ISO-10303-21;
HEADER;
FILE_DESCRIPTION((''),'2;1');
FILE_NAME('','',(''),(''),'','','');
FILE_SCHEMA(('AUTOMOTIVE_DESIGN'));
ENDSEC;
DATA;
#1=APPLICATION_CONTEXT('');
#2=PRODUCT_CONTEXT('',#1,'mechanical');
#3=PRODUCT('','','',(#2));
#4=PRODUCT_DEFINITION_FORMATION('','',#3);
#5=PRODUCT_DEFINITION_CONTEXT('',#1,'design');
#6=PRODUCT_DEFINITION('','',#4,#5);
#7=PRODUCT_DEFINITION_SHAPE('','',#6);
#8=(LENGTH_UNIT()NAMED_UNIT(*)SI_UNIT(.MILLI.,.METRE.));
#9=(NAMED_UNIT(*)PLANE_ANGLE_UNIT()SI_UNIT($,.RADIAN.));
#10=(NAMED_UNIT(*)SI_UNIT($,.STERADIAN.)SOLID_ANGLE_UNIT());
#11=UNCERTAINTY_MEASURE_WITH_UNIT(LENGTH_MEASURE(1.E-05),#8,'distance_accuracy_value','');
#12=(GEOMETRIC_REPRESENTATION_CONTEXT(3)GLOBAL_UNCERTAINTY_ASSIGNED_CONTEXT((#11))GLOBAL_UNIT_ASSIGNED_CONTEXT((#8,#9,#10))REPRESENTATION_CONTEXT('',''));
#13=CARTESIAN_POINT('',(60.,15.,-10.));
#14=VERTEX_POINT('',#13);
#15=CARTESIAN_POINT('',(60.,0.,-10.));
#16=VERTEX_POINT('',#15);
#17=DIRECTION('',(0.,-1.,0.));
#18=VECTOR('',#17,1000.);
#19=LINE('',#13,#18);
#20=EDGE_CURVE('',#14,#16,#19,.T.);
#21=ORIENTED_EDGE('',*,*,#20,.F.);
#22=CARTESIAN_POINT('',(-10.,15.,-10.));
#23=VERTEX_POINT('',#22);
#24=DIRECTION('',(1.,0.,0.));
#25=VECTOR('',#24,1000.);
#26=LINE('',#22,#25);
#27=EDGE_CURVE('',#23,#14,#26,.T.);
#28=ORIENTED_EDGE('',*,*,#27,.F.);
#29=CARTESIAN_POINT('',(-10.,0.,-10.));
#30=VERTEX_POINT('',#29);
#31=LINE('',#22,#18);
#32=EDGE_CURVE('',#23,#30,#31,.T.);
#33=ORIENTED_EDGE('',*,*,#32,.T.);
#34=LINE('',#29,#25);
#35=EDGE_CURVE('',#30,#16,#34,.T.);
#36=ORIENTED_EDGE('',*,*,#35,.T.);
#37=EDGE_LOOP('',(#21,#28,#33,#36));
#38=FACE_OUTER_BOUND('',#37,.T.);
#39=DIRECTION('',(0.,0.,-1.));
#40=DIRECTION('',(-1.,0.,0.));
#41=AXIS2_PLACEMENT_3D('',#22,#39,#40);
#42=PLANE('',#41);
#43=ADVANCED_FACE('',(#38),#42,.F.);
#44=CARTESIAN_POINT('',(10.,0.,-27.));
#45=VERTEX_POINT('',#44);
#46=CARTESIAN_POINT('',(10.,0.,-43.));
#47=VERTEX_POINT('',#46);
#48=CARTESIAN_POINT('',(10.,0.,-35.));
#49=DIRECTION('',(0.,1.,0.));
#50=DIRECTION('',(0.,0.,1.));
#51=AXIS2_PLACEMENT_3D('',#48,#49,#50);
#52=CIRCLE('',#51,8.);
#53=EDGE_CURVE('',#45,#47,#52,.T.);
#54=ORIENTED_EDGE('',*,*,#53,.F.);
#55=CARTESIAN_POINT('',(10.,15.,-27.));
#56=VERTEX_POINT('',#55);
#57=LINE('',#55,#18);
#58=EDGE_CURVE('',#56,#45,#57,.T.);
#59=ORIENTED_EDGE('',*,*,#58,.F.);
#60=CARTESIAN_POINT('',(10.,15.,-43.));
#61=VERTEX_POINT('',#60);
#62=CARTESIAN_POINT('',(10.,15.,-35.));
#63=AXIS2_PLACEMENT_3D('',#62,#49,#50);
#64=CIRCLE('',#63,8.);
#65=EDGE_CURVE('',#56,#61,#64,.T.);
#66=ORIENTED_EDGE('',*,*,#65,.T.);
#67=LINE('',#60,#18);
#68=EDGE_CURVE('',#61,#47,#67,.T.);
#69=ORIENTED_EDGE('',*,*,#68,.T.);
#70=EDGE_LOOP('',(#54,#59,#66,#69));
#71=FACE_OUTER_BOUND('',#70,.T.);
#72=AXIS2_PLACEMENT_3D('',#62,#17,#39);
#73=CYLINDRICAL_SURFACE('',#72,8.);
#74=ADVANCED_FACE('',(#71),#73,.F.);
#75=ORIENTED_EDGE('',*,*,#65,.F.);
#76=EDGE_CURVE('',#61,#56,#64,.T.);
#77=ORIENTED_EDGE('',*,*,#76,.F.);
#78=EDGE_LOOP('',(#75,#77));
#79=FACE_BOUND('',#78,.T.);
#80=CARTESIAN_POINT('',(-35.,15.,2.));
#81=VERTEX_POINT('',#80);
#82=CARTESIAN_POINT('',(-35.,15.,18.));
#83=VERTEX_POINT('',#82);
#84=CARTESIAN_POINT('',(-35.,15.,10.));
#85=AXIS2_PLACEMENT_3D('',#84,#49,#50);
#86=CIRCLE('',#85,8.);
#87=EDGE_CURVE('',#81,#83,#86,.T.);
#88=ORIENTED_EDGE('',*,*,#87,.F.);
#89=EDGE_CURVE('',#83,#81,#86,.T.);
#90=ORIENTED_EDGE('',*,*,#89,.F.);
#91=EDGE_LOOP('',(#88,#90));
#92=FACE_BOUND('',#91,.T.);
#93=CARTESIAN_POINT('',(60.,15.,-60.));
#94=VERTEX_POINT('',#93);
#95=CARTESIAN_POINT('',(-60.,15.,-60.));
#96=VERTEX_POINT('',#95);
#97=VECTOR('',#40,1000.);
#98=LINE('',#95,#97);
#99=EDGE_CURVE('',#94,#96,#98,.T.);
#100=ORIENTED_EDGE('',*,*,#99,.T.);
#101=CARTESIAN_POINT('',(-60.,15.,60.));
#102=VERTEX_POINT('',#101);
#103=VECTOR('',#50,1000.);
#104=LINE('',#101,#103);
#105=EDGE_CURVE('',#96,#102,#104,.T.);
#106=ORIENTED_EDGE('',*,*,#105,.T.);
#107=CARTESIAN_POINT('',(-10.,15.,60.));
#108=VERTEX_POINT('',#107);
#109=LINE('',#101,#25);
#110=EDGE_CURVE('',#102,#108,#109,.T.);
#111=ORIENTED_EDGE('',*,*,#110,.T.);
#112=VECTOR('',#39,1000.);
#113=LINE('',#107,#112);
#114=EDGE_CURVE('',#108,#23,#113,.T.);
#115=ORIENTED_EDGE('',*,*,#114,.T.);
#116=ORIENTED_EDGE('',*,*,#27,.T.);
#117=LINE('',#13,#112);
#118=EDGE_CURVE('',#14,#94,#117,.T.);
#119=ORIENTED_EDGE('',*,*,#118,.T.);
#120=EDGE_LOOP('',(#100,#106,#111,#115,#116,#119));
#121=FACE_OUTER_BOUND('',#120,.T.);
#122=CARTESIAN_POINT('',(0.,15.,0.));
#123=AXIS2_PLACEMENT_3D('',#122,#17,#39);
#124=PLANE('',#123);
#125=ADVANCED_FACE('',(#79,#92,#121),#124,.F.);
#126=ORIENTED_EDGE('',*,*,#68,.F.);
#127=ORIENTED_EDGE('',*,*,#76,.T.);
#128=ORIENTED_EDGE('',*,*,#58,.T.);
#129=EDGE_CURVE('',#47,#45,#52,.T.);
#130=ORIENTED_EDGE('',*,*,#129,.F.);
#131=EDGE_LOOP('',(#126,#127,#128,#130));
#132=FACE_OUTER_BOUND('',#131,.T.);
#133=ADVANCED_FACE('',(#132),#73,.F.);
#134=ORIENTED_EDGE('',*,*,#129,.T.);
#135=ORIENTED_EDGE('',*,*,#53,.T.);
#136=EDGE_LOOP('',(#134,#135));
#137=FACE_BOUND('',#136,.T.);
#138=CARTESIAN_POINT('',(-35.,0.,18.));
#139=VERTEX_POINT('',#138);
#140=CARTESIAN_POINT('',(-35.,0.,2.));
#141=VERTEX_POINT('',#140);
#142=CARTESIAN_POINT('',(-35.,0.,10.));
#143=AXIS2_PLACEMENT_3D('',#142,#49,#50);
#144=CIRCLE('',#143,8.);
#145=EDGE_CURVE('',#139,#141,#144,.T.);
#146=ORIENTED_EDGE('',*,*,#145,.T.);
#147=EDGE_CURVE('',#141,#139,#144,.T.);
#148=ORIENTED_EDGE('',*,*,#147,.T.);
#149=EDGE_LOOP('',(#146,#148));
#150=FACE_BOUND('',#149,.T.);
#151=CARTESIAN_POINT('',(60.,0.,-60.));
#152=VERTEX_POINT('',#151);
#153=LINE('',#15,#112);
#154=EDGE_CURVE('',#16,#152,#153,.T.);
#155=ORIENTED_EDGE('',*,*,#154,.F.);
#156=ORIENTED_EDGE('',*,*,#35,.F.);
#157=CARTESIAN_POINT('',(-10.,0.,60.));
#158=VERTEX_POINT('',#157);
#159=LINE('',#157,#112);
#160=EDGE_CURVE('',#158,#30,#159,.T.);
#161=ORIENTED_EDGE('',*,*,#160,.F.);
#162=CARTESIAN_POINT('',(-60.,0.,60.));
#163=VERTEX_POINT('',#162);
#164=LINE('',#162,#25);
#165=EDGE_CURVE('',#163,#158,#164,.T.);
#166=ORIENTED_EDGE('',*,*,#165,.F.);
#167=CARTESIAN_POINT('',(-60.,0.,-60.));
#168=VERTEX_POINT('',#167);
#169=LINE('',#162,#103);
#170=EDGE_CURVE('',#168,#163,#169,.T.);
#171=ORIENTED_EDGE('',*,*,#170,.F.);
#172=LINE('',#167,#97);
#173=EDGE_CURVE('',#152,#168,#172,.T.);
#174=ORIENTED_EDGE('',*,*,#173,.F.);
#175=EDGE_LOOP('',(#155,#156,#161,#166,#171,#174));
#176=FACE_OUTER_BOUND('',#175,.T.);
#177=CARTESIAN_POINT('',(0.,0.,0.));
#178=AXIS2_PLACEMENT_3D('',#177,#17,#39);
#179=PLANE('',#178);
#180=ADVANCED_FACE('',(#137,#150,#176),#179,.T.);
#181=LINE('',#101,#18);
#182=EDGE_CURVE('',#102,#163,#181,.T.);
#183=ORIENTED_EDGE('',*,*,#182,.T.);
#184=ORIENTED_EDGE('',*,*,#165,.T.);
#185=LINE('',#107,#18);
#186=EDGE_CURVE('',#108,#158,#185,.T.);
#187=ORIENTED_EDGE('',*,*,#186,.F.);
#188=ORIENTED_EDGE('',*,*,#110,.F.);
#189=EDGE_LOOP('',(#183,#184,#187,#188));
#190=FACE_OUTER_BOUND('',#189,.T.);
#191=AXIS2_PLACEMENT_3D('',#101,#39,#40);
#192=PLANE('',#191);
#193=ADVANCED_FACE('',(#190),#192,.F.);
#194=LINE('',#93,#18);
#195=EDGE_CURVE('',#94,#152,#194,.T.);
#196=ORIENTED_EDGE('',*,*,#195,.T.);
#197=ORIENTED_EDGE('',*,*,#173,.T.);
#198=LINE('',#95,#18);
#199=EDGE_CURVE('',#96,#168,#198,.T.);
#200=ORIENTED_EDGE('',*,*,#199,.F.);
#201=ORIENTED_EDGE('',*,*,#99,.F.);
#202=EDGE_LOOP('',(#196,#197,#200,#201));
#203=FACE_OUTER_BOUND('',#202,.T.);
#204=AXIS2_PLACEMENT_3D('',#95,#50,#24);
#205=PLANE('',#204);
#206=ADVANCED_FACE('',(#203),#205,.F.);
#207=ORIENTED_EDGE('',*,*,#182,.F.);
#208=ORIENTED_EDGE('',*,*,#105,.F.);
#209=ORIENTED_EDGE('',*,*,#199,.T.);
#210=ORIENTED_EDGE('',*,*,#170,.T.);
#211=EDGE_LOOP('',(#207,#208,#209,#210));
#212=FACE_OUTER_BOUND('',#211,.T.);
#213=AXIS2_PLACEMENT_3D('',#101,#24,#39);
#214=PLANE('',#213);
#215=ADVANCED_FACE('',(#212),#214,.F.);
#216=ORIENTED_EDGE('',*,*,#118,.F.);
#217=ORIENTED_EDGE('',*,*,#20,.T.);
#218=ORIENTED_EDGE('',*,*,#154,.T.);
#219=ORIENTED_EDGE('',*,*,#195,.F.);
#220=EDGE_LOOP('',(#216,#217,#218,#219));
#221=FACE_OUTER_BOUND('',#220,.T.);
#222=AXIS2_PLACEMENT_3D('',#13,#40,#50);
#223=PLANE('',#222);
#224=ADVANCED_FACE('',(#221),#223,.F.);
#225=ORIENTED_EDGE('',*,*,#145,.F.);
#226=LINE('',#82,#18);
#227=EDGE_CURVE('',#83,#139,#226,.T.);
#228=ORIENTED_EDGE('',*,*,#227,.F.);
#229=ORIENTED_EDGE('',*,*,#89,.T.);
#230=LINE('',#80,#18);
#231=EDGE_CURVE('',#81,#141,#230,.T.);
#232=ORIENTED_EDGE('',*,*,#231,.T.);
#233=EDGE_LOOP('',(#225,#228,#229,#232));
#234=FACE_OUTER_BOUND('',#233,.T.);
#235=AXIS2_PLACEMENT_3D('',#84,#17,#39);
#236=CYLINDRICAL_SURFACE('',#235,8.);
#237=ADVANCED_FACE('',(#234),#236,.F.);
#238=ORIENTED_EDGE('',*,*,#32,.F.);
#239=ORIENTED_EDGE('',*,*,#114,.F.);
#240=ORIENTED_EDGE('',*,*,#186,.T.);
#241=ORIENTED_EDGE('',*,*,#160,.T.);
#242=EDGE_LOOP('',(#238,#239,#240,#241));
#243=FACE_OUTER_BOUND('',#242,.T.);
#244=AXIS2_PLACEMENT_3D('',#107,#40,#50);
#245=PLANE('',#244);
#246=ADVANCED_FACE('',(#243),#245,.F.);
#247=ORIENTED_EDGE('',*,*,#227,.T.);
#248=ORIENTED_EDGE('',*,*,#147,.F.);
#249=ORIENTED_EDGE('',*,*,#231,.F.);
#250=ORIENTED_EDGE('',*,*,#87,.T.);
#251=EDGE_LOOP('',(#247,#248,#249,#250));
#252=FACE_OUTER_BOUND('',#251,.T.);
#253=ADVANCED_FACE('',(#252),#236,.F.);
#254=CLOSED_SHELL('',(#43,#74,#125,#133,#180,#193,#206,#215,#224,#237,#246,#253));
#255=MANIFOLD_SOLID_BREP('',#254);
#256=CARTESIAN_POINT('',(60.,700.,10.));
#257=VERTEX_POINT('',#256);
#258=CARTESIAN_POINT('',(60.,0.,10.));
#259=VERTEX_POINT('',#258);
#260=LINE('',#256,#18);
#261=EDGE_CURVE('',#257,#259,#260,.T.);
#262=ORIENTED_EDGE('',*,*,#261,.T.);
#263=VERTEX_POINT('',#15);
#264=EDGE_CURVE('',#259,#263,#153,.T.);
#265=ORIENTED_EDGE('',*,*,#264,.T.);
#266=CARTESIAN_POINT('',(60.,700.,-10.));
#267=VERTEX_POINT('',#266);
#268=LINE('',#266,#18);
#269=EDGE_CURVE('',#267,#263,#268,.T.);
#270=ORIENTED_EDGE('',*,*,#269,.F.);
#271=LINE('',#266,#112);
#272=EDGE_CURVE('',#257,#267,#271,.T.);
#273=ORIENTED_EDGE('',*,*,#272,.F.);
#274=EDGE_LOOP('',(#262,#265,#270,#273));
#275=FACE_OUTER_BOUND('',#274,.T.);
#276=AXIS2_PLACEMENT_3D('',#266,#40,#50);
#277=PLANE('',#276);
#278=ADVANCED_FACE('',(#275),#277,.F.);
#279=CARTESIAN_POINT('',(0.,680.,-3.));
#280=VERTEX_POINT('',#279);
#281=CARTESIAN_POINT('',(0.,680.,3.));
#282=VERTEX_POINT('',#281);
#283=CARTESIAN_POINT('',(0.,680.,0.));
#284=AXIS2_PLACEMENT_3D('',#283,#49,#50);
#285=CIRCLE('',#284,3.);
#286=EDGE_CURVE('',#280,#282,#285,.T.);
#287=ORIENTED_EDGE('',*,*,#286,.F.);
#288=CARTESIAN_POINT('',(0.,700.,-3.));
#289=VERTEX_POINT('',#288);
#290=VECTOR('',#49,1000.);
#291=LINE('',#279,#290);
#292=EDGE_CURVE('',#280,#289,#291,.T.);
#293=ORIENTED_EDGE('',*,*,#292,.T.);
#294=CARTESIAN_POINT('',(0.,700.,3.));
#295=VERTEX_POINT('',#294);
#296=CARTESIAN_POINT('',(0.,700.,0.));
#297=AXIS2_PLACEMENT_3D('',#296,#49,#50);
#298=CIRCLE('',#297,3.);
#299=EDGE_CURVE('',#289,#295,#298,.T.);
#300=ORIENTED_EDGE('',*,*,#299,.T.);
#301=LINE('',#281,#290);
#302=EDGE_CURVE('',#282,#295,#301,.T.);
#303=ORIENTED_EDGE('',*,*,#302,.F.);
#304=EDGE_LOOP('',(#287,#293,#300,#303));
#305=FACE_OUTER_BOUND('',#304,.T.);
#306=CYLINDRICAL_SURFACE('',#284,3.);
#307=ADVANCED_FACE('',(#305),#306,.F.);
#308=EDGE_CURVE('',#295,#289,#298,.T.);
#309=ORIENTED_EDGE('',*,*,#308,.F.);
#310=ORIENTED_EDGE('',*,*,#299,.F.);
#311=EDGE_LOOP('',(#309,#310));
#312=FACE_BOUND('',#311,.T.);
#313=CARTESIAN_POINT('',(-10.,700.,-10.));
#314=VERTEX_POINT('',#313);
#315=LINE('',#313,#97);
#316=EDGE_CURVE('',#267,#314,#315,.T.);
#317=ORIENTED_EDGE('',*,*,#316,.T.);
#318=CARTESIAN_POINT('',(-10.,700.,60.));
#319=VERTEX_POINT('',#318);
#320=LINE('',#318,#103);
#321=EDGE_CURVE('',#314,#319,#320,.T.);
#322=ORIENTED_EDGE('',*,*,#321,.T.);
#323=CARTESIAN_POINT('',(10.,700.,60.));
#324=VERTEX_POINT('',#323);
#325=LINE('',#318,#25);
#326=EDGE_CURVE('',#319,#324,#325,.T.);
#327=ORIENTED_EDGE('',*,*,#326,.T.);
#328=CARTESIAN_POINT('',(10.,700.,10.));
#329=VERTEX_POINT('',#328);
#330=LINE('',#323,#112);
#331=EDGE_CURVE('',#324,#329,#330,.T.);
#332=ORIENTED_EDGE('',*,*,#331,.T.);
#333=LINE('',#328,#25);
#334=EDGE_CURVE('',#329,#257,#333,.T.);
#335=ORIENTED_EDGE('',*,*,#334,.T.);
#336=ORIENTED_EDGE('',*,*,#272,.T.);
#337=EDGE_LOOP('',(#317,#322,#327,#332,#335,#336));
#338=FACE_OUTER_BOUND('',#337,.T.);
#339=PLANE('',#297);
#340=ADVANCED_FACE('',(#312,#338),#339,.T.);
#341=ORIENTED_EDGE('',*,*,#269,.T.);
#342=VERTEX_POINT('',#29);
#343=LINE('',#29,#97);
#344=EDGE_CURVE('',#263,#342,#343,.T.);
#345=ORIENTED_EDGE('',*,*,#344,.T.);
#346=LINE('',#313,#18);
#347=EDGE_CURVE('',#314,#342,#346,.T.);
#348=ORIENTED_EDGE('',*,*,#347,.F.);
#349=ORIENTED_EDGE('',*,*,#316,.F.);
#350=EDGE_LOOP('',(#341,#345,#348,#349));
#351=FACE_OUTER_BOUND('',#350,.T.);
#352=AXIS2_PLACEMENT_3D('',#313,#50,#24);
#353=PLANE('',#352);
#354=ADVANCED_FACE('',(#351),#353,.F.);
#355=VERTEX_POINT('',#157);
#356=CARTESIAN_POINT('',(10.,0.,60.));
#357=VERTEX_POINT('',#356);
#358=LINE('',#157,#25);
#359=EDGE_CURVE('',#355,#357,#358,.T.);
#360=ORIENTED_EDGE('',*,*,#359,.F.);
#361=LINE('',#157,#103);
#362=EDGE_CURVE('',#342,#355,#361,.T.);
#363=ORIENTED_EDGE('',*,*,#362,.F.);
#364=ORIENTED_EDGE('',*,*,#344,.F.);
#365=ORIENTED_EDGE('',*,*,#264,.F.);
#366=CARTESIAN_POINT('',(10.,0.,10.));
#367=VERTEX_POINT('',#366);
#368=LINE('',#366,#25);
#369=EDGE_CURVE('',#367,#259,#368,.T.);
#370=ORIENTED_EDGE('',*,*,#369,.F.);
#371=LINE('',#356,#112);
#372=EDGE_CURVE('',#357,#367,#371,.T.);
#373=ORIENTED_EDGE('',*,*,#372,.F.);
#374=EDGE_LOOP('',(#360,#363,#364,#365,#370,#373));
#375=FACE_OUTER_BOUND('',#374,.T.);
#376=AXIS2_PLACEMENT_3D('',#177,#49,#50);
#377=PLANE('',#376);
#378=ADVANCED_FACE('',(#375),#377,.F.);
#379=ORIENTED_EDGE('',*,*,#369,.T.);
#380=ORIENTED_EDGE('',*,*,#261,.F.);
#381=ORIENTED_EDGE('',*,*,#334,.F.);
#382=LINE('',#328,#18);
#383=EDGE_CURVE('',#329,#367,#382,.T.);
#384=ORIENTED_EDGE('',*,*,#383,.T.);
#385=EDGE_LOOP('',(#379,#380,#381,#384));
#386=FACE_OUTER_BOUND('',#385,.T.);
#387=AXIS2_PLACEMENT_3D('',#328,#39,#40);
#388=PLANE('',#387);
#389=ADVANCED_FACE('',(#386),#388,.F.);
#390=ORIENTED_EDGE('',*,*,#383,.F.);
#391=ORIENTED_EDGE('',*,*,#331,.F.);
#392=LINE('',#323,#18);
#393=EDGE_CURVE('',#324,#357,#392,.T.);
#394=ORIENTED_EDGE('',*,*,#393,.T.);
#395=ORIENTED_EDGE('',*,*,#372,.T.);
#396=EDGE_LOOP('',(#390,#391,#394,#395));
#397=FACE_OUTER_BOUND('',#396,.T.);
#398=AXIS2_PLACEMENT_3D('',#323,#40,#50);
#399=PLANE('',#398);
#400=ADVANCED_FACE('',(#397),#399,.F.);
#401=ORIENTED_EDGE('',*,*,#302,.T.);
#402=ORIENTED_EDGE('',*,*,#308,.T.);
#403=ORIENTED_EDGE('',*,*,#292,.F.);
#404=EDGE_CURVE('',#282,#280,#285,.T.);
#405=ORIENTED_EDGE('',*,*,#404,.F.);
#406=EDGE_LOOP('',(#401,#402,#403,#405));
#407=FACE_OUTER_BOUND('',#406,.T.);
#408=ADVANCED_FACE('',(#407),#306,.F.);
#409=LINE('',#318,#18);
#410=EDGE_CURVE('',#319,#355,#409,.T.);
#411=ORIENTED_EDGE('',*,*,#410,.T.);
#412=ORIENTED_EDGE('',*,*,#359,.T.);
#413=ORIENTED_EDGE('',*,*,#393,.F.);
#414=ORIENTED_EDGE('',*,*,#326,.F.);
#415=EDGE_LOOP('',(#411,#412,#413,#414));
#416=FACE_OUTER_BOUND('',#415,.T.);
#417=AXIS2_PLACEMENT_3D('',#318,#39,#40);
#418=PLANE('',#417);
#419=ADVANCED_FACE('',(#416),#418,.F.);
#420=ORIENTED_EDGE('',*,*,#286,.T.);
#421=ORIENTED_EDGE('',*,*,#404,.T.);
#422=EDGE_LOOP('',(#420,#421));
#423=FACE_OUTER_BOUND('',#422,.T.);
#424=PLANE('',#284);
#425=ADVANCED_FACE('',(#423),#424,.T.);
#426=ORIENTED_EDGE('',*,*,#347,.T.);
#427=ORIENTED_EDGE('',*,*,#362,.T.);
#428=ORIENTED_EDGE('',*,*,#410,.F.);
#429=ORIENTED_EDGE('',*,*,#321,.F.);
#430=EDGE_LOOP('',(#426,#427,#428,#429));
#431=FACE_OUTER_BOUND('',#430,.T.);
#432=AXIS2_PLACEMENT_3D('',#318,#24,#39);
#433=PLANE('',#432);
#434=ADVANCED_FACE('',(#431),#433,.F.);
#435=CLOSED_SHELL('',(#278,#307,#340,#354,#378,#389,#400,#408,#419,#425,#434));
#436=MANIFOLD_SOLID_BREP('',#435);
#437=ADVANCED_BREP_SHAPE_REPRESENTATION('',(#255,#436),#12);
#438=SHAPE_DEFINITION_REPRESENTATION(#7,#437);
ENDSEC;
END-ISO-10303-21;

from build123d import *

# Parameters (mm, degrees)
SKETCH2_R                = 8
BOSS_EXTRUDE1_DEPTH      = 15
BOSS_EXTRUDE2_DEPTH      = 685
BOSS_EXTRUDE2_DEPTH_BACK = 15
SKETCH4_R                = 3
CUT_EXTRUDE1_DEPTH       = 20


with BuildPart() as part:
    # Sketch2 → Boss-Extrude1 (new body)
    with BuildSketch(Plane(origin=(0, 0, 0), x_dir=(1, 0, 0), z_dir=(0, 1, 0))):
        Polygon((-60, -60), (-10, -60), (-10, 10), (60, 10), (60, 60), (-60, 60), align=None)
        with Locations(Location((-35, -10, 0), (0, 0, 270))):
            Circle(SKETCH2_R, mode=Mode.SUBTRACT)
        with Locations(Location((10, 35, 0), (0, 0, 270))):
            Circle(SKETCH2_R, mode=Mode.SUBTRACT)
    extrude(amount=BOSS_EXTRUDE1_DEPTH)


with BuildPart() as body_2:
    # Sketch3 → Boss-Extrude2 (new, two sides: drawn at the far end of the back side and taken through both)
    with BuildSketch(Plane(origin=(0, 15, 0), x_dir=(1, 0, 0), z_dir=(0, 1, 0)).offset(-BOSS_EXTRUDE2_DEPTH_BACK)):
        Polygon((-10, -60), (-10, 10), (60, 10), (60, -10), (10, -10), (10, -60), align=None)
    extrude(amount=BOSS_EXTRUDE2_DEPTH + BOSS_EXTRUDE2_DEPTH_BACK)

    # Sketch4 → Cut-Extrude1 (cut)
    with BuildSketch(Plane(origin=(0, 700, 0), x_dir=(1, 0, 0), z_dir=(0, 1, 0))):
        with Locations(Location((0, 0, 0), (0, 0, 270))):
            Circle(SKETCH4_R)
    extrude(amount=-CUT_EXTRUDE1_DEPTH, mode=Mode.SUBTRACT)


solid = Compound([part.part, body_2.part])
